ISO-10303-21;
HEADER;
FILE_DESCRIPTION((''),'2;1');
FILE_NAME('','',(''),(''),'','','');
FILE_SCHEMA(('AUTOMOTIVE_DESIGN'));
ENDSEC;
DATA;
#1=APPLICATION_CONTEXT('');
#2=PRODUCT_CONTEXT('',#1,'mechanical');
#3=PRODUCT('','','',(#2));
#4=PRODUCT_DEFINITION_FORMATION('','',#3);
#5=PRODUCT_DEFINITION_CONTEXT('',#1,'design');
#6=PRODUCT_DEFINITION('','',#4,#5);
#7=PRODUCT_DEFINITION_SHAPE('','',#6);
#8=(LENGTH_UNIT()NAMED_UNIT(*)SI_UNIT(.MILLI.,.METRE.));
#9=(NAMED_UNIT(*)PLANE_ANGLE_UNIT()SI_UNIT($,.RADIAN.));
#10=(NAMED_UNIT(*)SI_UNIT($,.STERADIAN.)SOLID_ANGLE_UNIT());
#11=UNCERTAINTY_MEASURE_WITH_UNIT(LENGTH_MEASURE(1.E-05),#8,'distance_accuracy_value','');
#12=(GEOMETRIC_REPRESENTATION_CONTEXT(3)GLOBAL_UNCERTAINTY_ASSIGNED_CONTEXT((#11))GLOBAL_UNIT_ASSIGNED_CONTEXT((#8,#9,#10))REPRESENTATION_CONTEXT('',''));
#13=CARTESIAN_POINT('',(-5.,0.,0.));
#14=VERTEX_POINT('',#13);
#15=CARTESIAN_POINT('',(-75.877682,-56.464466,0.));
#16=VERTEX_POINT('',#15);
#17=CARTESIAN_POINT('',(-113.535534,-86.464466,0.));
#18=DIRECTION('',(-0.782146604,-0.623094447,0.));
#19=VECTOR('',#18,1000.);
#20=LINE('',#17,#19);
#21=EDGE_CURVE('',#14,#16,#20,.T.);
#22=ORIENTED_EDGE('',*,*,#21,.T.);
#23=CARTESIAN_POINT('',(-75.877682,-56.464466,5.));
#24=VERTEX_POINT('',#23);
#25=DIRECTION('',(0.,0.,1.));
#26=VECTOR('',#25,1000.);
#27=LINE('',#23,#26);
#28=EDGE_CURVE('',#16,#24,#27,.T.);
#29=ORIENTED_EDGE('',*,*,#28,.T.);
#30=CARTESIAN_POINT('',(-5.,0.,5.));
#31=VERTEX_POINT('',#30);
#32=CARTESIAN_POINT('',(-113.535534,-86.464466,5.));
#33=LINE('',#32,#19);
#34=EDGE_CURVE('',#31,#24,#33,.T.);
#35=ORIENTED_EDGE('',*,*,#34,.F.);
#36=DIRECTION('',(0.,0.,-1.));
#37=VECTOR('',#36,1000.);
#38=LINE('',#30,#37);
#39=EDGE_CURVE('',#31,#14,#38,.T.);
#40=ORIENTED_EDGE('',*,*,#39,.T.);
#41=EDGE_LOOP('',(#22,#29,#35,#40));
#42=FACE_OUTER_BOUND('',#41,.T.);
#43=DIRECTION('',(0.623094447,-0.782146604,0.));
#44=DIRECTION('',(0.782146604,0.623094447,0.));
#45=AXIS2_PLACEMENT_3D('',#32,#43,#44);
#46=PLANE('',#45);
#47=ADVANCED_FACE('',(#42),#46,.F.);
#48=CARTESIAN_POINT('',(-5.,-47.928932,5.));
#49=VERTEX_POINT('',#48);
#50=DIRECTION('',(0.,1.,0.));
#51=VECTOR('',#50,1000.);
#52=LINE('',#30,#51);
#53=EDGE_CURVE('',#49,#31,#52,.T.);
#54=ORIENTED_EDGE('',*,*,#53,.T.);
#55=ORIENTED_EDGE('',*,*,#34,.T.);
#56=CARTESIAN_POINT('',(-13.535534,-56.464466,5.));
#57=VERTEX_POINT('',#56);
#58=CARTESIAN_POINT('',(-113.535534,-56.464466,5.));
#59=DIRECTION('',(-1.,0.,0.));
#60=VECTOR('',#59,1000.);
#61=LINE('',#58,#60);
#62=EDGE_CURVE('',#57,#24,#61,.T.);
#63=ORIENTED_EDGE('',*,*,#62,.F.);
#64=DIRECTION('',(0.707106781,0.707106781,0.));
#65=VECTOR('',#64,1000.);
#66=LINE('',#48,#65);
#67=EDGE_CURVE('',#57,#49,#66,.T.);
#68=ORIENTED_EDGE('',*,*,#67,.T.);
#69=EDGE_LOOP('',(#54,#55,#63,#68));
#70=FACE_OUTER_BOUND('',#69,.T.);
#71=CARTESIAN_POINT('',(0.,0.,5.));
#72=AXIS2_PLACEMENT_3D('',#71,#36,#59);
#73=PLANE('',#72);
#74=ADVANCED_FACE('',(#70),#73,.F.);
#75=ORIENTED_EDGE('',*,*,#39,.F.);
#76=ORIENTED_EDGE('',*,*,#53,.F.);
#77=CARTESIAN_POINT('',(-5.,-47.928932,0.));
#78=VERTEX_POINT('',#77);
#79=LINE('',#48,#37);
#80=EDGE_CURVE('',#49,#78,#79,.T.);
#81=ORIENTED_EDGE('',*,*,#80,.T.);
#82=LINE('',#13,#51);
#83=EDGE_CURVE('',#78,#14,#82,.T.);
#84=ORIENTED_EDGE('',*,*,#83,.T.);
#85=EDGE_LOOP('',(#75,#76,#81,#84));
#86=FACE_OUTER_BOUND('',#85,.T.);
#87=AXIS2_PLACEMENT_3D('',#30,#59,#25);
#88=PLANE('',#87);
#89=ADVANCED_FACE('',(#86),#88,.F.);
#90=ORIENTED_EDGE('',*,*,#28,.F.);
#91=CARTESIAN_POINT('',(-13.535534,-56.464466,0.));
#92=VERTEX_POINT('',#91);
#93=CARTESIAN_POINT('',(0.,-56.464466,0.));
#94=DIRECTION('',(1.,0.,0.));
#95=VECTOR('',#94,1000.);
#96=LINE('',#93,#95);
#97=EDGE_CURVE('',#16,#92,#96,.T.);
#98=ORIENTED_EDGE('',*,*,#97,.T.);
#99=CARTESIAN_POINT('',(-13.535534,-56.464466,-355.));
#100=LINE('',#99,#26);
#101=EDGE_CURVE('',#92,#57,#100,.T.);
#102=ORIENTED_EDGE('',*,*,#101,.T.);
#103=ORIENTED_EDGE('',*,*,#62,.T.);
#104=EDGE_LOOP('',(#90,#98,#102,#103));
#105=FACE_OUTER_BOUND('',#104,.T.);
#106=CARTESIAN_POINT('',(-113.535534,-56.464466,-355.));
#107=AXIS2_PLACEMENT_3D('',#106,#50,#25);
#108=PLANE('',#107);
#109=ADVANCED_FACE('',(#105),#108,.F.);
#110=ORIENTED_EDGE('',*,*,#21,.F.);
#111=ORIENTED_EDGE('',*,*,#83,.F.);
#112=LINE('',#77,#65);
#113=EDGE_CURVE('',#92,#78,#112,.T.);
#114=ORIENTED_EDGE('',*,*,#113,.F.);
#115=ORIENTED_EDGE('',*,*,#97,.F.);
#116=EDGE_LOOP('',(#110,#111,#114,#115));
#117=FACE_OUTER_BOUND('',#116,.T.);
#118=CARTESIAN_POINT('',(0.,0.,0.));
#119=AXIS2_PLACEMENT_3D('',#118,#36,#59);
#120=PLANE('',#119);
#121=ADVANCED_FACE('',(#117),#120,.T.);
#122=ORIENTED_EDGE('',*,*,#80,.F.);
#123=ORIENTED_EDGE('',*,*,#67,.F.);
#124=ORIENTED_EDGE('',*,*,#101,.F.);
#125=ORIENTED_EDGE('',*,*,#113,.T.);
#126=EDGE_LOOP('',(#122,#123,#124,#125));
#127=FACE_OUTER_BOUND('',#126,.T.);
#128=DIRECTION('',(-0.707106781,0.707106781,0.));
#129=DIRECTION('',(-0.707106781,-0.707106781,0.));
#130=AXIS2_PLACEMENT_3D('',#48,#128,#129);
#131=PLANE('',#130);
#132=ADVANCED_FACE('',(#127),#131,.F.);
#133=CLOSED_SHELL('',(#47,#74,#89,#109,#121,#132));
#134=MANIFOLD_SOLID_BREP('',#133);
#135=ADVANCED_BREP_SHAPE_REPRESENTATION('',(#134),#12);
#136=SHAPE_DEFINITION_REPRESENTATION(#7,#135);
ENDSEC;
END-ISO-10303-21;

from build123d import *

# Parameters (mm, degrees)
EXTRUDE_1_DEPTH     = 5
SKETCH_2_W          = 100
SKETCH_2_H          = 30
CUT_EXTRUDE_1_DEPTH = 360


with BuildPart() as part:
    # 草图1 → 凸台-拉伸1 (new body)
    with BuildSketch(Plane.XY):
        Polygon((-5, 0), (-5, -47.928932188), (-43.535533906, -86.464466094), (-113.535533906, -86.464466094), align=None)
    extrude(amount=EXTRUDE_1_DEPTH)

    # 草图2 → 切除-拉伸1 (cut)
    with BuildSketch(Plane.XY.offset(5)):
        with Locations((-63.535533906, -71.464466094)):
            Rectangle(SKETCH_2_W, SKETCH_2_H)
    extrude(amount=-CUT_EXTRUDE_1_DEPTH, mode=Mode.SUBTRACT)


solid = part.part
